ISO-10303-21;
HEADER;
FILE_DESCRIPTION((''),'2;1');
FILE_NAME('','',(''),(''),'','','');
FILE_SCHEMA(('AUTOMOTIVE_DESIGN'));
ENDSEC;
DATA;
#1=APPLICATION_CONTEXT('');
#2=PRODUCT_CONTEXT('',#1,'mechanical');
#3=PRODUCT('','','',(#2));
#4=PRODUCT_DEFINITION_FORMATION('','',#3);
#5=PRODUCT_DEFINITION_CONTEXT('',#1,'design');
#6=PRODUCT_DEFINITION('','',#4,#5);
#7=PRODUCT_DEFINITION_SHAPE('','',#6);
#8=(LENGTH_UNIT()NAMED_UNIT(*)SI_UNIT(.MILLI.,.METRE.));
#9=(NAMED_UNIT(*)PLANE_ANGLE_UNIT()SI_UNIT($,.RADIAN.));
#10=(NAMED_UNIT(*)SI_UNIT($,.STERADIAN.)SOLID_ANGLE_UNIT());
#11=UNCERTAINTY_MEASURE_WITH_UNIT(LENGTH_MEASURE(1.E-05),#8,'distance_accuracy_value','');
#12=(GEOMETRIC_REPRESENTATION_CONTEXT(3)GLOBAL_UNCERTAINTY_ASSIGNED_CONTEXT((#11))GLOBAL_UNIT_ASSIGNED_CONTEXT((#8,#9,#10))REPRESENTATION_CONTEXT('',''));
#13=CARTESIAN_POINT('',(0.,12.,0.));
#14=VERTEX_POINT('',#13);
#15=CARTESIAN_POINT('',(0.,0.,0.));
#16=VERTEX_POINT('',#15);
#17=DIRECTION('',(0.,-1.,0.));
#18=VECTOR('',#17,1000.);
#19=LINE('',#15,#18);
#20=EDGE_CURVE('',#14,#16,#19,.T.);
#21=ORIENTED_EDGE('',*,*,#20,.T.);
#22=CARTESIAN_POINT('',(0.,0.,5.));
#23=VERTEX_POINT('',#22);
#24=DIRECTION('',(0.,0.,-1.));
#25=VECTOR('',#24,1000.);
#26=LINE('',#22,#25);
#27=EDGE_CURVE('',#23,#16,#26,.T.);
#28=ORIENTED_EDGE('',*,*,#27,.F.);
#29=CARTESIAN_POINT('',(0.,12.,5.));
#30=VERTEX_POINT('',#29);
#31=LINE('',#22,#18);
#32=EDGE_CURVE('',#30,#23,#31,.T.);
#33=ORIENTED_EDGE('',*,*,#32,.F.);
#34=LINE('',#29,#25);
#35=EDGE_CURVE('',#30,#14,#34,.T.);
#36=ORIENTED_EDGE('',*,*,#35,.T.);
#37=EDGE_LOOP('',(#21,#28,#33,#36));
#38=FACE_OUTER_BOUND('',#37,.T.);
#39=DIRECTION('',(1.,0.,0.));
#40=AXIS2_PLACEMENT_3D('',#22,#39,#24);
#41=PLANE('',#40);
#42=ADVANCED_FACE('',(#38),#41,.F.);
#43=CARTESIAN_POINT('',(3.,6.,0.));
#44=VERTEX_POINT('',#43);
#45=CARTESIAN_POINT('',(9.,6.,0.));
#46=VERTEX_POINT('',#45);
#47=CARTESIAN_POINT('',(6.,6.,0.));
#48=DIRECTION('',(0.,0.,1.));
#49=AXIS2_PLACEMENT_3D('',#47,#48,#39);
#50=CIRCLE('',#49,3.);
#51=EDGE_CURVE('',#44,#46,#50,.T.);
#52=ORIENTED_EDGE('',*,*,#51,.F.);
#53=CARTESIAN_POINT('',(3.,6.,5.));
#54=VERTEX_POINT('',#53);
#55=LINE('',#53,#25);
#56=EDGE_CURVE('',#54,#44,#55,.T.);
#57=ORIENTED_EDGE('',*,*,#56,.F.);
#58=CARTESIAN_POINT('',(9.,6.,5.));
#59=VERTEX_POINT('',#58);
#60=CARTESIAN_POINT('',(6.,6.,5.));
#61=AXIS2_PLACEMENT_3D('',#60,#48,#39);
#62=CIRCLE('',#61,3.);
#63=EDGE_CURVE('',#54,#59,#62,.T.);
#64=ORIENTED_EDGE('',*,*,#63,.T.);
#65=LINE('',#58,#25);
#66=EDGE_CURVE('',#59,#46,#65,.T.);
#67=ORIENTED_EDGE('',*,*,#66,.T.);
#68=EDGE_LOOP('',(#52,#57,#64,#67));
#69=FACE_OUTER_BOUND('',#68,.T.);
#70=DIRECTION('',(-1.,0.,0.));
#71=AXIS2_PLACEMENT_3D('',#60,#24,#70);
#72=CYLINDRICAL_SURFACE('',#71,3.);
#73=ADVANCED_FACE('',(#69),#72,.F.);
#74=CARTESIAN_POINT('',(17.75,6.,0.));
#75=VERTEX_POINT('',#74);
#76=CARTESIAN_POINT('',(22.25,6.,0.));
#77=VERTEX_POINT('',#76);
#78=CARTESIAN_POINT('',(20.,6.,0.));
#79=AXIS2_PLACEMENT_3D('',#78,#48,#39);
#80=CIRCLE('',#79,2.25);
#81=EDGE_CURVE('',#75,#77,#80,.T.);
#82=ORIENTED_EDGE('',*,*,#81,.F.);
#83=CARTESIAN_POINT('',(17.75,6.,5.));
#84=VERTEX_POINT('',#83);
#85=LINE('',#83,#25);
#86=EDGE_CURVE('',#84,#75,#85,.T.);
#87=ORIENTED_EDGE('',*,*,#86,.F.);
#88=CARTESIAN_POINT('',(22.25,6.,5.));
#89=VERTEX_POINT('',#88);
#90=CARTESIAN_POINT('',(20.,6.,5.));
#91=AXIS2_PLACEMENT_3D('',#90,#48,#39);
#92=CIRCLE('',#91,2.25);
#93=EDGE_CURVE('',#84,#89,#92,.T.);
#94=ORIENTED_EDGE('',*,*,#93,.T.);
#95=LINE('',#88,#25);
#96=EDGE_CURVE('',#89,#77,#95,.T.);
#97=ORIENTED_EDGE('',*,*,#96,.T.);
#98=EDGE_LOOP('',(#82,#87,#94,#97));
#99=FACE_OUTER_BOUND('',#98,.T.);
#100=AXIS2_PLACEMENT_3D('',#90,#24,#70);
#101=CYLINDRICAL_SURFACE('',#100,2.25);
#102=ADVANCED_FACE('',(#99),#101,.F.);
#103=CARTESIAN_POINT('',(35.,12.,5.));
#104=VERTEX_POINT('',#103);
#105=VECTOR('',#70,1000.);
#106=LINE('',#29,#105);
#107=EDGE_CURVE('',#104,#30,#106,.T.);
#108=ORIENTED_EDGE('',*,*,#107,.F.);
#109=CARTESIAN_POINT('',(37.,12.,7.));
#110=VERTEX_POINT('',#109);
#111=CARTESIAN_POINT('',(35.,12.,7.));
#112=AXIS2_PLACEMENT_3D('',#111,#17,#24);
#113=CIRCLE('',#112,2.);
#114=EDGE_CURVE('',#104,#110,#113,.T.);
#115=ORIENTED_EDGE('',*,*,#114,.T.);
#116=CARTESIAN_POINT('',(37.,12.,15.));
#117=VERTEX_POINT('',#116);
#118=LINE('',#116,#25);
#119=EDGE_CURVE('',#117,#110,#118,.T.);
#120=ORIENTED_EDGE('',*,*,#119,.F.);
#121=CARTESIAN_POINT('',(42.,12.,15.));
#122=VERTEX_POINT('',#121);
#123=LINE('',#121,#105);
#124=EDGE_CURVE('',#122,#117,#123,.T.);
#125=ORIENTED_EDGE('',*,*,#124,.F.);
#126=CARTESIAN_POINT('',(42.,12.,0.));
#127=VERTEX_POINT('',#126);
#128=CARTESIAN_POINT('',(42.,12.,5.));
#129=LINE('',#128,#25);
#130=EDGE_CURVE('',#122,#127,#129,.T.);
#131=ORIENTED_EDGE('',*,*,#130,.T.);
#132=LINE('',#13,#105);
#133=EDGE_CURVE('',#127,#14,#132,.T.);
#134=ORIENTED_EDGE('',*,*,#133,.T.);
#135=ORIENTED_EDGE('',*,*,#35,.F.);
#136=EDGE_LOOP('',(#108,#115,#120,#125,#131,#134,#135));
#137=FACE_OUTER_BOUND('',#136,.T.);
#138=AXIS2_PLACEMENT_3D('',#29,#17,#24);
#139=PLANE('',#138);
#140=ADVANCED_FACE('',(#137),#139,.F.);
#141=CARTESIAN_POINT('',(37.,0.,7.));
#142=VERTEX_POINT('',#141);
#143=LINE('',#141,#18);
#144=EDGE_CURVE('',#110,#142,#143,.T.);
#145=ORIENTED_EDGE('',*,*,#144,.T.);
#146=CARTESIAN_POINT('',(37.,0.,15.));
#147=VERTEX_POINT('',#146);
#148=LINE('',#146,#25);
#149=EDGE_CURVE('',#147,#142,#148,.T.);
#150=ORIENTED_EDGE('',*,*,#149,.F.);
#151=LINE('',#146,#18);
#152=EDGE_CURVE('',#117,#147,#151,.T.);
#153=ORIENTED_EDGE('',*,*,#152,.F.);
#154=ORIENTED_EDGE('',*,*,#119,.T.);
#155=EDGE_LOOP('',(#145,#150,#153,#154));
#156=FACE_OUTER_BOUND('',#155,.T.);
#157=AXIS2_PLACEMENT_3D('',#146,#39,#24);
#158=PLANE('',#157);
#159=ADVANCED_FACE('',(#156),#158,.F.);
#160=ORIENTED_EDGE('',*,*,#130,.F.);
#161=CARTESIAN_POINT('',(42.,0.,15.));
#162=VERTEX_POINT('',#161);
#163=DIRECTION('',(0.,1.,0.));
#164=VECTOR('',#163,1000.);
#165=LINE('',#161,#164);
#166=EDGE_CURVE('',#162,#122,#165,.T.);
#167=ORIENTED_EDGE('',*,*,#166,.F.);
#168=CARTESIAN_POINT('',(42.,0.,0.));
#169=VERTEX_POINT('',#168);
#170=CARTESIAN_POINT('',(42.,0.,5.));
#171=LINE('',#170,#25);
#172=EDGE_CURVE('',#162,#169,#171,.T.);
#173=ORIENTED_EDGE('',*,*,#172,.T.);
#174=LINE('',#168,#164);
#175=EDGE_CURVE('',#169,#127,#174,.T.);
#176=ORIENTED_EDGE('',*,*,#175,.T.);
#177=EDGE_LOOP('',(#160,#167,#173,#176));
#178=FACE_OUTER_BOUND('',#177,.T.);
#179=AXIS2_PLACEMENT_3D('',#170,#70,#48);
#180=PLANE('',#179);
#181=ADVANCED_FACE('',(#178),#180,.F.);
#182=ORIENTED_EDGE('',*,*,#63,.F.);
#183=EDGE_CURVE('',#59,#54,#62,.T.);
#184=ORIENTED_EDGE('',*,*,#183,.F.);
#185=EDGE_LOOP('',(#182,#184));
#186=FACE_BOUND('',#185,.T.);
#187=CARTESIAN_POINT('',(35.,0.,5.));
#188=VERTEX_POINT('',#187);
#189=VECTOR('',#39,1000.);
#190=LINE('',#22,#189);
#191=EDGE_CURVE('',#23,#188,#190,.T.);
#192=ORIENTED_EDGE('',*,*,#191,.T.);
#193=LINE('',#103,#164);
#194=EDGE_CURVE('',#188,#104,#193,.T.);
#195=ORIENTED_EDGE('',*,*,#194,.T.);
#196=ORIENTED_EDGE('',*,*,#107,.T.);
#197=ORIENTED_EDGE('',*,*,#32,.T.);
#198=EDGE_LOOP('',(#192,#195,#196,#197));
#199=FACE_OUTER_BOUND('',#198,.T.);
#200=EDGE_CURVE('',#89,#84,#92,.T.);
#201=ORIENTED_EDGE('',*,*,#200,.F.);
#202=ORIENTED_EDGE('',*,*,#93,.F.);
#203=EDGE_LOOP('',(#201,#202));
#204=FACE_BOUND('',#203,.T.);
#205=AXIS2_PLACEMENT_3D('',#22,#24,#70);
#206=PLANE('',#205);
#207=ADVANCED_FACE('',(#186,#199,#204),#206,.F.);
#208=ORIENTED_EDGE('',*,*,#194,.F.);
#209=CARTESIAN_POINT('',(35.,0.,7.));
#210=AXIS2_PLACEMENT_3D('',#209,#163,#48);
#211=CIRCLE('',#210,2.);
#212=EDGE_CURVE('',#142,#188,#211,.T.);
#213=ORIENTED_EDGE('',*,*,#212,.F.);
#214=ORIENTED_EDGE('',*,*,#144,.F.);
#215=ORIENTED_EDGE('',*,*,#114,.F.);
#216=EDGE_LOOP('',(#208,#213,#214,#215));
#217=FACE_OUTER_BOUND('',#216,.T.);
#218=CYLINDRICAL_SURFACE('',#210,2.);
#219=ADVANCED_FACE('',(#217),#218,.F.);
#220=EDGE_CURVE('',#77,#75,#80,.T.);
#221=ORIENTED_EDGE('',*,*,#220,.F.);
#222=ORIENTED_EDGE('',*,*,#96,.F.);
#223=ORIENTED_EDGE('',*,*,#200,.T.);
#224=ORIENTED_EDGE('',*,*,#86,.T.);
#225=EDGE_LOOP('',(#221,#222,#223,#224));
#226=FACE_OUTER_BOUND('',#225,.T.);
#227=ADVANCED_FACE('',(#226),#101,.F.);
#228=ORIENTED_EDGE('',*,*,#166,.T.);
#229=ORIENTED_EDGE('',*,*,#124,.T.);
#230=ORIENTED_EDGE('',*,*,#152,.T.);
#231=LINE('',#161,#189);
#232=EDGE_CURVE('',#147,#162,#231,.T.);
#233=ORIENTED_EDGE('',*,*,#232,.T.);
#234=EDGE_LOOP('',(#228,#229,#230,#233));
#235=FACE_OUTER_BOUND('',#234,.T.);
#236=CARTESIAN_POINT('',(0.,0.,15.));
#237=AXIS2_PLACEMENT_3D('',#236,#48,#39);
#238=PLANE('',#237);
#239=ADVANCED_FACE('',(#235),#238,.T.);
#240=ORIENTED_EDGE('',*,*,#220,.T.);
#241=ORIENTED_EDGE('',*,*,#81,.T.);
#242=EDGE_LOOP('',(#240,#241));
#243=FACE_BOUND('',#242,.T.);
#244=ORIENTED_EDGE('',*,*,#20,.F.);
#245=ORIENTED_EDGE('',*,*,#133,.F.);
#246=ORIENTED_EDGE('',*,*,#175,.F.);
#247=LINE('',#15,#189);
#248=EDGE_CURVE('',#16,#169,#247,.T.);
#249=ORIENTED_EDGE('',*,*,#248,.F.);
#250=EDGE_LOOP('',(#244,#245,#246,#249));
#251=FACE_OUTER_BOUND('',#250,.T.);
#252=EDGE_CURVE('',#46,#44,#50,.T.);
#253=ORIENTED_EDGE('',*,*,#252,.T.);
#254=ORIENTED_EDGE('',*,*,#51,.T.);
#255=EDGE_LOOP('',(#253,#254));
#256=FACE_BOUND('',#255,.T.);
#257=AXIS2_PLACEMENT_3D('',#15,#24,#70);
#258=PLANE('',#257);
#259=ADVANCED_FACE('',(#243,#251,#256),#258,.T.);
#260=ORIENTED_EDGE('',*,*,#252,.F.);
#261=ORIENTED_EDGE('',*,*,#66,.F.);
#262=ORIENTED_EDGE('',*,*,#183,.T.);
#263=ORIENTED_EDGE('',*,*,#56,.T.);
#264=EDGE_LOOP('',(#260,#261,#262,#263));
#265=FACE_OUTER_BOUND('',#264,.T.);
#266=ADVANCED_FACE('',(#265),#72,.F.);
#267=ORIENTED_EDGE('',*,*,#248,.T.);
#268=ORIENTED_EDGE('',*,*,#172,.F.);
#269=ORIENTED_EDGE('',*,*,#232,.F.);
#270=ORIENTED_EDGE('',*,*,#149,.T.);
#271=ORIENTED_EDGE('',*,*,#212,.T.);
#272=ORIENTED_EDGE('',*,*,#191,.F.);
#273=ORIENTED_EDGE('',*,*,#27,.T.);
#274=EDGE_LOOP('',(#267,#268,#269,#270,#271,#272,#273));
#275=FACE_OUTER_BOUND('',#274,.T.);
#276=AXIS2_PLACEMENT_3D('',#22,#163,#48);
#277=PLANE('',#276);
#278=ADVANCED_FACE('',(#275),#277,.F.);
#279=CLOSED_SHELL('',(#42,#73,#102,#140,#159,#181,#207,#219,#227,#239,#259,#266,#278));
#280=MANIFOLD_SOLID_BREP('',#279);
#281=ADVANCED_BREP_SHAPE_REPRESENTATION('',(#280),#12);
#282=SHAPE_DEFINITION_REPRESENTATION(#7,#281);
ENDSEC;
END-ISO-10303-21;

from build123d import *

# Parameters (mm, degrees)
SKETCH1_W           = 42
SKETCH1_H           = 12
SKETCH1_R           = 2.25
SKETCH1_R_2         = 3
BOSS_EXTRUDE1_DEPTH = 5
SKETCH2_W           = 5
SKETCH2_H           = 12
BOSS_EXTRUDE2_DEPTH = 10
FILLET1_R           = 2


with BuildPart() as part:
    # Sketch1 → Boss-Extrude1 (new body)
    with BuildSketch(Plane.XY):
        with Locations((21, 6)):
            Rectangle(SKETCH1_W, SKETCH1_H)
        with Locations((20, 6)):
            Circle(SKETCH1_R, mode=Mode.SUBTRACT)
        with Locations((6, 6)):
            Circle(SKETCH1_R_2, mode=Mode.SUBTRACT)
    extrude(amount=BOSS_EXTRUDE1_DEPTH)

    # Sketch2 → Boss-Extrude2 (add)
    with BuildSketch(Plane.XY.offset(5)):
        with Locations((39.5, 6)):
            Rectangle(SKETCH2_W, SKETCH2_H)
    extrude(amount=BOSS_EXTRUDE2_DEPTH)

    # Fillet1
    fillet1_edges = [part.edges().sort_by_distance(p)[0] for p in [
        (37, 6, 5),
    ]]
    fillet(fillet1_edges, radius=FILLET1_R)


solid = part.part
